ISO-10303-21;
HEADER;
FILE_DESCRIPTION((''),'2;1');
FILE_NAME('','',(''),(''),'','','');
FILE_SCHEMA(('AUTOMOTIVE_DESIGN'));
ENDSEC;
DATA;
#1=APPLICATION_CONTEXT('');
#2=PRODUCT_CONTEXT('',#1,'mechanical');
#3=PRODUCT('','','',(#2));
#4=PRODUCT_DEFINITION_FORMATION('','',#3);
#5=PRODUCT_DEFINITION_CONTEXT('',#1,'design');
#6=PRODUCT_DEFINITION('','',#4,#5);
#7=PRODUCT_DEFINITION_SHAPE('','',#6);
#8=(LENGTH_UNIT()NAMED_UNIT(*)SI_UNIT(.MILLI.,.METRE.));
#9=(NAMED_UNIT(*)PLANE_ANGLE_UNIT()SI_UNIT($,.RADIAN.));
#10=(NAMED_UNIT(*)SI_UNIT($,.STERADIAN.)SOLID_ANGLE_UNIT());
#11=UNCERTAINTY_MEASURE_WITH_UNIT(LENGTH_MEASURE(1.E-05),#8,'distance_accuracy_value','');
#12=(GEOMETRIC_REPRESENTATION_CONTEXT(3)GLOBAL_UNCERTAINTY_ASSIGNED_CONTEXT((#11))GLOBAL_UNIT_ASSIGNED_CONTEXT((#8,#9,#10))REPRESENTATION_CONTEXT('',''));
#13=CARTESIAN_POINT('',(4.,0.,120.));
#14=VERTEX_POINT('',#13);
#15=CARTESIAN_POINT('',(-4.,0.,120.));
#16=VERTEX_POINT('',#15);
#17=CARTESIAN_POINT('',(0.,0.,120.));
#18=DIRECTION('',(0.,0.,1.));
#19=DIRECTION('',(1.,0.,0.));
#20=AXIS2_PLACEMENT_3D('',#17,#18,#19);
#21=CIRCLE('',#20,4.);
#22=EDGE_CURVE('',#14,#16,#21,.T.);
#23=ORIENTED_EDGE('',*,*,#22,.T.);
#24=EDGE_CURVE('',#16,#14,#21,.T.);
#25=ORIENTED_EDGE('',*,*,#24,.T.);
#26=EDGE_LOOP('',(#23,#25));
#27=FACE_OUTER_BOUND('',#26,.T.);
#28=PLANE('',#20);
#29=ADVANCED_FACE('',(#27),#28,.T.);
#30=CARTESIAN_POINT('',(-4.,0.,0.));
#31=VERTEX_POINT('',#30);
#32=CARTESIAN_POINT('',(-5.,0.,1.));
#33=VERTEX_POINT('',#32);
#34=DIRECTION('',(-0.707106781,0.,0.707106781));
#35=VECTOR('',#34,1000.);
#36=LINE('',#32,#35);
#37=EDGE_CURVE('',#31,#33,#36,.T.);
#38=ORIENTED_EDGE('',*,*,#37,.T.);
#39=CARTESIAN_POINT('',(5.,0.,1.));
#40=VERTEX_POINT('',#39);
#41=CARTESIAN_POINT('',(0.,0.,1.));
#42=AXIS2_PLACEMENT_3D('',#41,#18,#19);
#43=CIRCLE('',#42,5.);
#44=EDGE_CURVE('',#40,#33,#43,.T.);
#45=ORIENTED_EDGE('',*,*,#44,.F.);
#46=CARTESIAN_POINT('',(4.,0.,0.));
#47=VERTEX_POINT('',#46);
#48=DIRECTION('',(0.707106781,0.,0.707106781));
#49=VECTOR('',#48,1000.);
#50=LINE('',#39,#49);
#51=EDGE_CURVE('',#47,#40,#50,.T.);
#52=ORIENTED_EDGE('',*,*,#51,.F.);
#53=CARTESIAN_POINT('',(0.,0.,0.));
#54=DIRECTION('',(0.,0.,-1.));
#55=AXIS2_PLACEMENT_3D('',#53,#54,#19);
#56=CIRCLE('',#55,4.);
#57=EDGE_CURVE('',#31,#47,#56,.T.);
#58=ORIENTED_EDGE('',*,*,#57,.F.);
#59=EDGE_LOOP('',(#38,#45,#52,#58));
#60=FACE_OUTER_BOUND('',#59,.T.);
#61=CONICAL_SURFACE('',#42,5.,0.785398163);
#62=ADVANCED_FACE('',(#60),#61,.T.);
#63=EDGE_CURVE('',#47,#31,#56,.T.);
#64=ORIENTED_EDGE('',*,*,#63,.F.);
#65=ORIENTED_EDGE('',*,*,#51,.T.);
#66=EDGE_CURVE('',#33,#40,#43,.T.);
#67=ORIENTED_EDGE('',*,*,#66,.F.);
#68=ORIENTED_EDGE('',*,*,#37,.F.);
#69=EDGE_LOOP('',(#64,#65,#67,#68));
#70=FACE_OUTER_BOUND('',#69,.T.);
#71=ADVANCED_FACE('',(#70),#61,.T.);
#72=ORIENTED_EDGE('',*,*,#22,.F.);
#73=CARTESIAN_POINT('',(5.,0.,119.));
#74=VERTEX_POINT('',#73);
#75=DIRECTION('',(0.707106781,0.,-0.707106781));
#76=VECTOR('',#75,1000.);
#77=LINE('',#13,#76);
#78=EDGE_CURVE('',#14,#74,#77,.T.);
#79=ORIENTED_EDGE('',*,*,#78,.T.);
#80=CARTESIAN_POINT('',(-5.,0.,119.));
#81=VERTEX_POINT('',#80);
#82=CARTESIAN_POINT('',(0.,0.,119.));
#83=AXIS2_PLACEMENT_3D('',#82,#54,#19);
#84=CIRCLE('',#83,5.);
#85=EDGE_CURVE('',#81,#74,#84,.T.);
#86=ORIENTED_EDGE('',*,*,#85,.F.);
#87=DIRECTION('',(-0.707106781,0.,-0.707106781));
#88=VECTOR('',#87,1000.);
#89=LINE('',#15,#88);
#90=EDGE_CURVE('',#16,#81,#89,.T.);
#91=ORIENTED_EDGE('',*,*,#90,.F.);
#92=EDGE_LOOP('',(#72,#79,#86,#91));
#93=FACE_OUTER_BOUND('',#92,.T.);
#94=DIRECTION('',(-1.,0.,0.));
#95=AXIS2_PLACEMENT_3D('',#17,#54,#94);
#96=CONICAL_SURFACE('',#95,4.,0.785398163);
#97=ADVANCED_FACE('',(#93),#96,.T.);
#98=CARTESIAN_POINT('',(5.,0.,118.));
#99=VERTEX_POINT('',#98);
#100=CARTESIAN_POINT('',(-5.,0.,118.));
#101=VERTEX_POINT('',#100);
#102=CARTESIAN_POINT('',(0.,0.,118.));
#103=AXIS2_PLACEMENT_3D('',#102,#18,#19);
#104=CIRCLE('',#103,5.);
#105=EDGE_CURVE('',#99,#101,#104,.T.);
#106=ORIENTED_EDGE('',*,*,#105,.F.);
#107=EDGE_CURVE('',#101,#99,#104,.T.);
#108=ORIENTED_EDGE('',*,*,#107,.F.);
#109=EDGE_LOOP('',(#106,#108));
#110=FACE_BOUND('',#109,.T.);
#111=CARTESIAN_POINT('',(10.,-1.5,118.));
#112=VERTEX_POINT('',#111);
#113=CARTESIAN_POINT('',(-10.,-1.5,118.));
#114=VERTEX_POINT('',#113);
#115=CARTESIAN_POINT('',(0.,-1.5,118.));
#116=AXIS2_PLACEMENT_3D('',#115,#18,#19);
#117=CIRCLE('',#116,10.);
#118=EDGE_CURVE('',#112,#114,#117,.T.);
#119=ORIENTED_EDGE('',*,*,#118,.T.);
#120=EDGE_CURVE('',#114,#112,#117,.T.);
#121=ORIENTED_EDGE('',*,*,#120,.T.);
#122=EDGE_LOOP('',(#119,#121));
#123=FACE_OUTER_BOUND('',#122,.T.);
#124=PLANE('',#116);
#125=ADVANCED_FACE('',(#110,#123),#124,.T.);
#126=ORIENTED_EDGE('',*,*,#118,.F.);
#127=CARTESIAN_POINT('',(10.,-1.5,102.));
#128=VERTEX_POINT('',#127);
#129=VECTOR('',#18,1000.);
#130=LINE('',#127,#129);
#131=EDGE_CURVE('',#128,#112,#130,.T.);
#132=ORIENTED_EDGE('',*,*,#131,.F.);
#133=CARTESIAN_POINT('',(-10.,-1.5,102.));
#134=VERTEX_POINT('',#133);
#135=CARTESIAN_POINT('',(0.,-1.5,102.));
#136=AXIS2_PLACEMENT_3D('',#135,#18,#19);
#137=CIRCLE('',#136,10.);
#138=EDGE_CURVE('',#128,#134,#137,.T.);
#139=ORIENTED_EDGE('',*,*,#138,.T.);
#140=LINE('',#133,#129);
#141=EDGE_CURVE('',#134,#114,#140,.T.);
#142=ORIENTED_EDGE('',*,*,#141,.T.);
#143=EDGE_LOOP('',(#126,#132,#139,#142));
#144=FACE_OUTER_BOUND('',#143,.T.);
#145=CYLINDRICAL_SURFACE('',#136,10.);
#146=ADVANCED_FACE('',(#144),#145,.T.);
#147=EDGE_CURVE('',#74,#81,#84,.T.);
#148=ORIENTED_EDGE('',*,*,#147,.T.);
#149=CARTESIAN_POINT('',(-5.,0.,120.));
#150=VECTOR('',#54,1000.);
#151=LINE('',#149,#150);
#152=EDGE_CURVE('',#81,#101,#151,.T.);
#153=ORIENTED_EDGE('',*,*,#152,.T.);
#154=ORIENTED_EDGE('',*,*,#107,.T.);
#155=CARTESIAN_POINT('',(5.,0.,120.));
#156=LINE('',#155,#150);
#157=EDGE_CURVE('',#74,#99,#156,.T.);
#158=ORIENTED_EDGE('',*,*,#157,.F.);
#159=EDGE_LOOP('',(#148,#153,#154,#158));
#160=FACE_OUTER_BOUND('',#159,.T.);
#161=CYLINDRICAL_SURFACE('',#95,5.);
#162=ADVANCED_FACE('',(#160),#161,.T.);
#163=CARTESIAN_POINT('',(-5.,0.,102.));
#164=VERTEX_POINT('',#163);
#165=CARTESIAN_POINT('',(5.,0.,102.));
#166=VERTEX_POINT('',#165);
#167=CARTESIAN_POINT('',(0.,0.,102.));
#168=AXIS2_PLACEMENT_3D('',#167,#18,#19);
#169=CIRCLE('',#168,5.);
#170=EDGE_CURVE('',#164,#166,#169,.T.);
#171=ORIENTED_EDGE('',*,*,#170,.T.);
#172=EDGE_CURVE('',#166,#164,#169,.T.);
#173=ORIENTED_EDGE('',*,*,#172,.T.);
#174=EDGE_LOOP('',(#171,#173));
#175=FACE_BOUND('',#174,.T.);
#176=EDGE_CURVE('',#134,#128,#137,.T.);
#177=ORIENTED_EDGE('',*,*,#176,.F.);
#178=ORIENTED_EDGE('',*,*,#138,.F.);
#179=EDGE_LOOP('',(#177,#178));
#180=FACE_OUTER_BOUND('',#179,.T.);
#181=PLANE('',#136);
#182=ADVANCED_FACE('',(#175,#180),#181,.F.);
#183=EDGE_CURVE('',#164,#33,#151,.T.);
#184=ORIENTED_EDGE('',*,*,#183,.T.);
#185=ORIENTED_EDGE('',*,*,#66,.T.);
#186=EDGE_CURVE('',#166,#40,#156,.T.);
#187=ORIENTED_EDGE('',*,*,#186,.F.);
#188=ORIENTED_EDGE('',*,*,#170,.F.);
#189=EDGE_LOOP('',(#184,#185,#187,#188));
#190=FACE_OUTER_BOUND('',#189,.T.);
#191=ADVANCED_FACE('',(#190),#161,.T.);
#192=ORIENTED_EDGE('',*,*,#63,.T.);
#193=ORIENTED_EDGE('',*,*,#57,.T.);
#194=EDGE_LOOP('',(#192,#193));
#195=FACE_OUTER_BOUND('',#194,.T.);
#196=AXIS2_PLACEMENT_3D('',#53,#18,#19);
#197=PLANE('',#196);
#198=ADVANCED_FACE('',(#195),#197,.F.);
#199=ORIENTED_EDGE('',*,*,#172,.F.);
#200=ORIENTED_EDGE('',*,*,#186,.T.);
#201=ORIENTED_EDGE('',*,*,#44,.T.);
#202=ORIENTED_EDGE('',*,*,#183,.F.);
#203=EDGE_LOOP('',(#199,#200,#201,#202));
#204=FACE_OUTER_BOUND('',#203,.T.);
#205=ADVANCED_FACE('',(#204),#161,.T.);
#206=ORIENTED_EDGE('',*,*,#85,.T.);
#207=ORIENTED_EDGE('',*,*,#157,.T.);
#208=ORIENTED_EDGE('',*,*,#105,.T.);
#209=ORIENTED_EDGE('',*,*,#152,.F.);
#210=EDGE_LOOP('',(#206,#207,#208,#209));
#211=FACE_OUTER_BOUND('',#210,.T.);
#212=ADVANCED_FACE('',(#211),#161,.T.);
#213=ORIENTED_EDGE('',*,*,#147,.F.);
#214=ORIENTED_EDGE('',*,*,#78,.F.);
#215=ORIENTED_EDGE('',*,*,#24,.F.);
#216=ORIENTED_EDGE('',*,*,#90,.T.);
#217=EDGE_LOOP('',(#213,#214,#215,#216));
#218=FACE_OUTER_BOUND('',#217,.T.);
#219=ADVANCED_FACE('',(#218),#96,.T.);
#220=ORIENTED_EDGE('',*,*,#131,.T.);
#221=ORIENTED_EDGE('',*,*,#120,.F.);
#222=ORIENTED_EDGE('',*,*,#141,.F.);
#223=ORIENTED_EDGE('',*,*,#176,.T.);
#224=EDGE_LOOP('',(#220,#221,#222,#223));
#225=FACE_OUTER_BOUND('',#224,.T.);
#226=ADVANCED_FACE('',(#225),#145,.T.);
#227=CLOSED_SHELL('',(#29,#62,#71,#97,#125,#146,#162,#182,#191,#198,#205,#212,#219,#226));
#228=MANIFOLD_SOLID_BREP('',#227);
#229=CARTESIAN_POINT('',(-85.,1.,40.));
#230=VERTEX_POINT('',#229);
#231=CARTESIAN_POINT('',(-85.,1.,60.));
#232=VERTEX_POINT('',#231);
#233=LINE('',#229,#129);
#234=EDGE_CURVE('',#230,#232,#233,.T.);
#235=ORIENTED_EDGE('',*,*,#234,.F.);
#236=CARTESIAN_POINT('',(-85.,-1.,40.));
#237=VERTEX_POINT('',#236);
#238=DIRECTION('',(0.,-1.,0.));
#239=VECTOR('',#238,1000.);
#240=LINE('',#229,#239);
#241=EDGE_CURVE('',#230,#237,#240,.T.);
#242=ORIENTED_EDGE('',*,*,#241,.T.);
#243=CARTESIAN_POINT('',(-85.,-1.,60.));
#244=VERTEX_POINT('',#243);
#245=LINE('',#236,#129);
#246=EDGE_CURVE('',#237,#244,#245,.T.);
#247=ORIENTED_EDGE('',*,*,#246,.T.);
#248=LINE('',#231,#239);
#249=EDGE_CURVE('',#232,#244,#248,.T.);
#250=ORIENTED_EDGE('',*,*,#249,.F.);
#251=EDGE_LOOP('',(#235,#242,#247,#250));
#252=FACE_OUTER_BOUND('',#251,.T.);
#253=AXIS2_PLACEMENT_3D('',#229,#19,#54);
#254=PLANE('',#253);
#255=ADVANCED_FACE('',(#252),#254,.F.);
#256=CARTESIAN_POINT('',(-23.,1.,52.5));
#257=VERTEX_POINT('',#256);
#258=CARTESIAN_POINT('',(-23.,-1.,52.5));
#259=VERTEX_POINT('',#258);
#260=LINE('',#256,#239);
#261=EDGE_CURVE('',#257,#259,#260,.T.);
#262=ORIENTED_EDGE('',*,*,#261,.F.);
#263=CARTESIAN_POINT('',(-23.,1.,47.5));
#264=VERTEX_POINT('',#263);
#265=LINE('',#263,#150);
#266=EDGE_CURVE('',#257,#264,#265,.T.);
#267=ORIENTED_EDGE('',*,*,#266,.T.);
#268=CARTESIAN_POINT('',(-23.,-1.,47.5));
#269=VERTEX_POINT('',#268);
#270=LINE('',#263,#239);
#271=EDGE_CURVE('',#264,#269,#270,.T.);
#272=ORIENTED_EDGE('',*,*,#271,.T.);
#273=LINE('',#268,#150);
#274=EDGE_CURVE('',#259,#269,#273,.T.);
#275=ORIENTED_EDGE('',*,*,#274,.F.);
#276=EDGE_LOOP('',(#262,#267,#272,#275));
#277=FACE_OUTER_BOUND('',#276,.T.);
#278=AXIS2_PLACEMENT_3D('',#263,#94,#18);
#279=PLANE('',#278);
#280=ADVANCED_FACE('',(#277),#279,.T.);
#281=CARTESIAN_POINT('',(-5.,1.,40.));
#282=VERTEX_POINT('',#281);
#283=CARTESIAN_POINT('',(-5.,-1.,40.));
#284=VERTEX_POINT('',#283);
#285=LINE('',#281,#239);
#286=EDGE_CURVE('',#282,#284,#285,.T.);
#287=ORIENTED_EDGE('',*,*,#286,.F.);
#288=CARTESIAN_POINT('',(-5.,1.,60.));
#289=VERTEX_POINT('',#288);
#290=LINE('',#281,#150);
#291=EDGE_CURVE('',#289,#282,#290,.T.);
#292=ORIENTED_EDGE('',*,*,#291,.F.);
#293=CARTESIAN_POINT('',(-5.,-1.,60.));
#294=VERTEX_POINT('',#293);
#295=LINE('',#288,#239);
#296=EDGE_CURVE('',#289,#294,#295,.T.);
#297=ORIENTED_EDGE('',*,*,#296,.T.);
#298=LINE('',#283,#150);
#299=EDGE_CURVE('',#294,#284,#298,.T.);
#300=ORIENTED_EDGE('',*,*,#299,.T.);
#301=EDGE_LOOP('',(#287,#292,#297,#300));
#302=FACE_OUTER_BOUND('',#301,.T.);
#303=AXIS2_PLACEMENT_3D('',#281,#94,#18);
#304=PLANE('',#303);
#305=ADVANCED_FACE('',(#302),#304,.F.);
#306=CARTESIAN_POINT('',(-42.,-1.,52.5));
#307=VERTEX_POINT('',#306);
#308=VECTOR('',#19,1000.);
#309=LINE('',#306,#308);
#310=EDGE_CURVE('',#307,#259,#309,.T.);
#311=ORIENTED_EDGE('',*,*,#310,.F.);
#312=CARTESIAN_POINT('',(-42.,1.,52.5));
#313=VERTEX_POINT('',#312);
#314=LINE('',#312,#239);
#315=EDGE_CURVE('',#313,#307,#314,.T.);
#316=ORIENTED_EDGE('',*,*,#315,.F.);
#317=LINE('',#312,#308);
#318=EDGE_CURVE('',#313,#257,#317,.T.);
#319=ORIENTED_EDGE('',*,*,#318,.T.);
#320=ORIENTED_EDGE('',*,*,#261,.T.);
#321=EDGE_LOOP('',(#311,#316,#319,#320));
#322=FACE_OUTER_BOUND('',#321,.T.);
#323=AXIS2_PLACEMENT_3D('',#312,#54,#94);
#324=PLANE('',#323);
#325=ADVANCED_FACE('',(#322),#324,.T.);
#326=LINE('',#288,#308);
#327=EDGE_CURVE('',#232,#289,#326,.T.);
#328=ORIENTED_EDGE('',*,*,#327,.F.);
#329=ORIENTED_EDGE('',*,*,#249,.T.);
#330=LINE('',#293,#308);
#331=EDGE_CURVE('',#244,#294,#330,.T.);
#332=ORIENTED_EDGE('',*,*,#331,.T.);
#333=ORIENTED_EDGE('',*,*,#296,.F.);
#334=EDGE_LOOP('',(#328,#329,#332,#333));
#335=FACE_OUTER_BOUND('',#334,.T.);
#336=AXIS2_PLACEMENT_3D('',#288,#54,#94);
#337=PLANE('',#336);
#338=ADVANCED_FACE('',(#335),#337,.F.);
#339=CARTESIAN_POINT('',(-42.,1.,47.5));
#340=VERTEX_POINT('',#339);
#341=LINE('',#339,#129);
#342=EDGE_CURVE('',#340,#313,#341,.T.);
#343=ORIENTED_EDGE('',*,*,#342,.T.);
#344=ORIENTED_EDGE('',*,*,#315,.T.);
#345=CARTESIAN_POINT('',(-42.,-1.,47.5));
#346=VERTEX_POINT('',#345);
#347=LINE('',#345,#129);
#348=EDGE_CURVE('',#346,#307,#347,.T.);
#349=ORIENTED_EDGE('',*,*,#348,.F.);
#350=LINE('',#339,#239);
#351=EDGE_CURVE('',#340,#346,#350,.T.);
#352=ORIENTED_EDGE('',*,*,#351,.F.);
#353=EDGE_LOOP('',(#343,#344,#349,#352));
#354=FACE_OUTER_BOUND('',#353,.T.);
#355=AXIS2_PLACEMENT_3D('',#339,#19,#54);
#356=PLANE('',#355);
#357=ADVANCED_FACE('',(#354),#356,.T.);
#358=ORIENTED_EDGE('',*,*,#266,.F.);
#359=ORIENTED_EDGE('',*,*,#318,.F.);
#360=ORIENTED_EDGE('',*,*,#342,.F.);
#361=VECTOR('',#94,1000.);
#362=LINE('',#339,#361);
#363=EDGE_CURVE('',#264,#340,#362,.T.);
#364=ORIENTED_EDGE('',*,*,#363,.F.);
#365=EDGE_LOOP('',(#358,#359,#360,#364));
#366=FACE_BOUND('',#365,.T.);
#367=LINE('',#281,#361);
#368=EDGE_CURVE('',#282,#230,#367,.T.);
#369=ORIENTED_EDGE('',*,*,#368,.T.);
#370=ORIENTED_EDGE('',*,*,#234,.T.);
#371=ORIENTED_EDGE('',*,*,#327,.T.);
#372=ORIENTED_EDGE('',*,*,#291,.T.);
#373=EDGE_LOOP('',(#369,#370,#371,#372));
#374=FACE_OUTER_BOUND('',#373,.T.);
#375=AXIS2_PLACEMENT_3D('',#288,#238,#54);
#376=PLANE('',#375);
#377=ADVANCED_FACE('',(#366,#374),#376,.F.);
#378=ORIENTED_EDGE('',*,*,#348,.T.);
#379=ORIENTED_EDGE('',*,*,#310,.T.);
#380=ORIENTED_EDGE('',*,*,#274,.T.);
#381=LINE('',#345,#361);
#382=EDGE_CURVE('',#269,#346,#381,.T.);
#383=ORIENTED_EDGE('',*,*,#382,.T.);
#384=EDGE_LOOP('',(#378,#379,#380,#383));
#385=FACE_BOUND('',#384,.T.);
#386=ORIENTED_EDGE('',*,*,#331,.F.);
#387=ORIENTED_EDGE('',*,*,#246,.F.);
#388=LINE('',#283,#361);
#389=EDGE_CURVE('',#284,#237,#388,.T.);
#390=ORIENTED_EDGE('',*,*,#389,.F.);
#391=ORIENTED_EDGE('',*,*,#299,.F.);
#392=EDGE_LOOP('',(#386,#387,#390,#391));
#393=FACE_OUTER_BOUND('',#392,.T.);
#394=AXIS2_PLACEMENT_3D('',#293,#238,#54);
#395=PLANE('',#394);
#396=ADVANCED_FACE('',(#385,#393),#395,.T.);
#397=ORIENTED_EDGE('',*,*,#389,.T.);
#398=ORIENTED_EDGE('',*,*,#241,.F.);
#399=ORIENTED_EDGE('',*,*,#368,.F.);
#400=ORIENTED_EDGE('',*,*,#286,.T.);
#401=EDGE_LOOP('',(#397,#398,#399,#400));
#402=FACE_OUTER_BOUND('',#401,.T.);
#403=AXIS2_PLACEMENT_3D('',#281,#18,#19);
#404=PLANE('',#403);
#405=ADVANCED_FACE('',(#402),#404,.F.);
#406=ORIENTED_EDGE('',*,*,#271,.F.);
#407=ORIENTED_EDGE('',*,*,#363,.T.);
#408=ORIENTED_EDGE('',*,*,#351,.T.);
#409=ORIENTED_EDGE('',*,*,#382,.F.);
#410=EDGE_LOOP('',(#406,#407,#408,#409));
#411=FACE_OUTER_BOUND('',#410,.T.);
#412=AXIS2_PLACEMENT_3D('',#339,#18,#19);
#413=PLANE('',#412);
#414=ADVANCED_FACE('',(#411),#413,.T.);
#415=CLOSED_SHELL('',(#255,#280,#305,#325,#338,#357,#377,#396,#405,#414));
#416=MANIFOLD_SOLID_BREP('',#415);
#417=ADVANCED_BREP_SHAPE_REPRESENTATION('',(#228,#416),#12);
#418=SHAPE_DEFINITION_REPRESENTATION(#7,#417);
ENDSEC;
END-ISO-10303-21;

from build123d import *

# Parameters (mm, degrees)
SKETCH_1_R      = 5
EXTRUDE_1_DEPTH = 120
EXTRUDE_START   = -2
SKETCH_2_R      = 10
EXTRUDE_2_DEPTH = 16
SKETCH_3_W      = 80
SKETCH_3_H      = 20
SKETCH_3_W_2    = 19
SKETCH_3_H_2    = 5
EXTRUDE_3_DEPTH = 1
CHAMFER_1_SIZE  = 1


with BuildPart() as part:
    # 草图1 → 凸台-拉伸1 (new body)
    with BuildSketch(Plane.XY):
        Circle(SKETCH_1_R)
    extrude(amount=EXTRUDE_1_DEPTH)

    # 草图2 → 凸台-拉伸2 (add)
    with BuildSketch(Plane.XY.offset(120).offset(EXTRUDE_START)):
        with Locations((0, -1.5)):
            Circle(SKETCH_2_R)
    extrude(amount=-EXTRUDE_2_DEPTH)

    # 倒角1
    chamfer_1_edges = [part.edges().sort_by_distance(p)[0] for p in [
        (-5, 0, 0),
        (-5, 0, 120),
    ]]
    chamfer(chamfer_1_edges, length=CHAMFER_1_SIZE)


with BuildPart() as body_2:
    # 草图3 → 凸台-拉伸3 (new, symmetric)
    with BuildSketch(Plane(origin=(0, 0, 0), x_dir=(1, 0, 0), z_dir=(0, 1, 0))):
        with Locations((-45, -50)):
            Rectangle(SKETCH_3_W, SKETCH_3_H)
        with Locations((-32.5, -50)):
            Rectangle(SKETCH_3_W_2, SKETCH_3_H_2, mode=Mode.SUBTRACT)
    extrude(amount=EXTRUDE_3_DEPTH, both=True)


solid = Compound([part.part, body_2.part])
